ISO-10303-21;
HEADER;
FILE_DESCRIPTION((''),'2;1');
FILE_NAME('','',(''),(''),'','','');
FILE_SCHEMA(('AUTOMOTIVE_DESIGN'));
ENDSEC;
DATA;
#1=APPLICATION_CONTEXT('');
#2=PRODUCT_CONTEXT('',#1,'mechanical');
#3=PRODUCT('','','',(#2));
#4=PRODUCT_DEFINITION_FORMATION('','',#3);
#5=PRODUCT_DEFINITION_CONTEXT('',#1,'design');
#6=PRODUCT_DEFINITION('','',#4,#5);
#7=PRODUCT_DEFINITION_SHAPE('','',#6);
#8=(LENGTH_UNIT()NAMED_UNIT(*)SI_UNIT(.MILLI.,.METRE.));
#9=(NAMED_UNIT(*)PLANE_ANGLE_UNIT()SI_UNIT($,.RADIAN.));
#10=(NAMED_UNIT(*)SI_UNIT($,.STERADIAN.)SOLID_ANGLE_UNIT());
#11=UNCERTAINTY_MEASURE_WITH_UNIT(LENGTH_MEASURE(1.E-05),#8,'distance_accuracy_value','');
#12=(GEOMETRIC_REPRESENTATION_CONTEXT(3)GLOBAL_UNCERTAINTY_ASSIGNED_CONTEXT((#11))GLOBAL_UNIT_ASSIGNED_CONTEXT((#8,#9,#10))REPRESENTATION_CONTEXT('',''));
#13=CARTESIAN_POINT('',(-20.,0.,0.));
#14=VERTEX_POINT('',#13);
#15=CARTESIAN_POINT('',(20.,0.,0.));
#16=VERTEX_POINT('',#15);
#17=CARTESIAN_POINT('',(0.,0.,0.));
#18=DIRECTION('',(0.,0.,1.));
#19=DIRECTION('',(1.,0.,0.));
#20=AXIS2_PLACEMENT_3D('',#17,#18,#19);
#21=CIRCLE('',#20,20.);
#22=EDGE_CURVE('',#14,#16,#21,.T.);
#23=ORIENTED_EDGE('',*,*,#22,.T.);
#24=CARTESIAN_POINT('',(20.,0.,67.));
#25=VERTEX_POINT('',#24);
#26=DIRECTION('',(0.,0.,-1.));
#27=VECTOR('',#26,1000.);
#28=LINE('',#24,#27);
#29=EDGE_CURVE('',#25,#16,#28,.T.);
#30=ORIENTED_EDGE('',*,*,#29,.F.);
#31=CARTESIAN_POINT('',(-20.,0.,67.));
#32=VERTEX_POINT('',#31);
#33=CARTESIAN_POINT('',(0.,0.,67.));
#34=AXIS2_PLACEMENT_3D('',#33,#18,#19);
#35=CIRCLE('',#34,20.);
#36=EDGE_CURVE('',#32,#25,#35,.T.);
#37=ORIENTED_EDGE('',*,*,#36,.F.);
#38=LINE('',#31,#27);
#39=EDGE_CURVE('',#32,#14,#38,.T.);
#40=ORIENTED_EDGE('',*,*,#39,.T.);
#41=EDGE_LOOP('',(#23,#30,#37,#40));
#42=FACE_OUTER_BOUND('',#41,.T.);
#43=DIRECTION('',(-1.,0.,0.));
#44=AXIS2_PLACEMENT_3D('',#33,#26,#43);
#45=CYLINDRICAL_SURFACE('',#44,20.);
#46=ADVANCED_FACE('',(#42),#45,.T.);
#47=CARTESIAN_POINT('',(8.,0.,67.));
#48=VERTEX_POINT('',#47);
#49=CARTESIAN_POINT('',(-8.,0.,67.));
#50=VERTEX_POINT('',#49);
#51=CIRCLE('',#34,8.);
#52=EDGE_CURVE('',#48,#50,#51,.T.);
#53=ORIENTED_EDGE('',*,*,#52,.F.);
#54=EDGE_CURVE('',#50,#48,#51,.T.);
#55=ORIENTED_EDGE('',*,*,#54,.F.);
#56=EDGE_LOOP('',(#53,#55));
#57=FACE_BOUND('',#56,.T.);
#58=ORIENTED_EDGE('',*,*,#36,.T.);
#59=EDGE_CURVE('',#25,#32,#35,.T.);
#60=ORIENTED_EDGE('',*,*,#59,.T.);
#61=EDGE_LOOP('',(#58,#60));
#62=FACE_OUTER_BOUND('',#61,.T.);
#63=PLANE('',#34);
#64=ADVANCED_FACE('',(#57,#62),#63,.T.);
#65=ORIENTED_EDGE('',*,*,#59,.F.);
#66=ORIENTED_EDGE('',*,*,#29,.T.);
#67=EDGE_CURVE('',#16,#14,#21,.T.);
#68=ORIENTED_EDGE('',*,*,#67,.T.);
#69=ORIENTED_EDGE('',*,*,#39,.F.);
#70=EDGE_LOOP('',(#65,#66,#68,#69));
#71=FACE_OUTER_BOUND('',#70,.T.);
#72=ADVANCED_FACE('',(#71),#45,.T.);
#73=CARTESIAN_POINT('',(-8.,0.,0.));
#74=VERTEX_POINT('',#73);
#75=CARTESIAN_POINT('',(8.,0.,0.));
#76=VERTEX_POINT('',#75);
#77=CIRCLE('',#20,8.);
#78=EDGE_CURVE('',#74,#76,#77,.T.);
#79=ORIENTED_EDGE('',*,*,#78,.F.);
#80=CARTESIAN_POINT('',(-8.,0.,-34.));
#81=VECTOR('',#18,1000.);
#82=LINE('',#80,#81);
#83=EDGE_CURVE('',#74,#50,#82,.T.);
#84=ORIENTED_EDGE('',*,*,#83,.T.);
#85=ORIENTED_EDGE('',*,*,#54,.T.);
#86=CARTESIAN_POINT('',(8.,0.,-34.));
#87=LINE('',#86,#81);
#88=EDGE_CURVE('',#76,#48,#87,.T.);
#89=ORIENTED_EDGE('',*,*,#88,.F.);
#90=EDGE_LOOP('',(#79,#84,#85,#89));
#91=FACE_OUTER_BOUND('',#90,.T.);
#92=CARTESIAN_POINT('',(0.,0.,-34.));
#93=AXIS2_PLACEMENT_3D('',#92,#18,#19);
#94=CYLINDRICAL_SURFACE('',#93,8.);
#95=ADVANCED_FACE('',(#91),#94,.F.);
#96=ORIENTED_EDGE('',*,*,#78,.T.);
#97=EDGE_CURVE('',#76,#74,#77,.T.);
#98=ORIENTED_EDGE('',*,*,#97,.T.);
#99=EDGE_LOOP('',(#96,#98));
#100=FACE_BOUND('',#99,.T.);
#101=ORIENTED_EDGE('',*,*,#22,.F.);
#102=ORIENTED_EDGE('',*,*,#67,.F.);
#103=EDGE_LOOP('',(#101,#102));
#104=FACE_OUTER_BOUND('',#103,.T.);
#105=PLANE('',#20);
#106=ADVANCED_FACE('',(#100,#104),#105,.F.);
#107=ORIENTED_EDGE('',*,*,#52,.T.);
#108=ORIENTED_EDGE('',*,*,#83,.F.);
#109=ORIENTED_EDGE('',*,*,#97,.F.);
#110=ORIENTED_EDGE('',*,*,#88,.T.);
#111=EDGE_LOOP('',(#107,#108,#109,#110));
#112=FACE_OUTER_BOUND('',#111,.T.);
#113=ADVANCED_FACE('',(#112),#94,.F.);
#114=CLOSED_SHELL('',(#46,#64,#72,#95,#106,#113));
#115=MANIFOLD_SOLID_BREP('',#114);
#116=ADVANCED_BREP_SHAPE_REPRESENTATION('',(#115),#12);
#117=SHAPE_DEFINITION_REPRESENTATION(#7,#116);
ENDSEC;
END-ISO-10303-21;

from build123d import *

# Parameters (mm, degrees)
SKETCH_1_R          = 20
EXTRUDE_1_DEPTH     = 67
SKETCH_2_R          = 8
CUT_EXTRUDE_1_DEPTH = 101


with BuildPart() as part:
    # 草图1 → 凸台-拉伸1 (new body)
    with BuildSketch(Plane.XY):
        Circle(SKETCH_1_R)
    extrude(amount=EXTRUDE_1_DEPTH)

    # 草图2 → 切除-拉伸1 (cut)
    with BuildSketch(Plane.XY.offset(67)):
        Circle(SKETCH_2_R)
    extrude(amount=-CUT_EXTRUDE_1_DEPTH, mode=Mode.SUBTRACT)


solid = part.part
